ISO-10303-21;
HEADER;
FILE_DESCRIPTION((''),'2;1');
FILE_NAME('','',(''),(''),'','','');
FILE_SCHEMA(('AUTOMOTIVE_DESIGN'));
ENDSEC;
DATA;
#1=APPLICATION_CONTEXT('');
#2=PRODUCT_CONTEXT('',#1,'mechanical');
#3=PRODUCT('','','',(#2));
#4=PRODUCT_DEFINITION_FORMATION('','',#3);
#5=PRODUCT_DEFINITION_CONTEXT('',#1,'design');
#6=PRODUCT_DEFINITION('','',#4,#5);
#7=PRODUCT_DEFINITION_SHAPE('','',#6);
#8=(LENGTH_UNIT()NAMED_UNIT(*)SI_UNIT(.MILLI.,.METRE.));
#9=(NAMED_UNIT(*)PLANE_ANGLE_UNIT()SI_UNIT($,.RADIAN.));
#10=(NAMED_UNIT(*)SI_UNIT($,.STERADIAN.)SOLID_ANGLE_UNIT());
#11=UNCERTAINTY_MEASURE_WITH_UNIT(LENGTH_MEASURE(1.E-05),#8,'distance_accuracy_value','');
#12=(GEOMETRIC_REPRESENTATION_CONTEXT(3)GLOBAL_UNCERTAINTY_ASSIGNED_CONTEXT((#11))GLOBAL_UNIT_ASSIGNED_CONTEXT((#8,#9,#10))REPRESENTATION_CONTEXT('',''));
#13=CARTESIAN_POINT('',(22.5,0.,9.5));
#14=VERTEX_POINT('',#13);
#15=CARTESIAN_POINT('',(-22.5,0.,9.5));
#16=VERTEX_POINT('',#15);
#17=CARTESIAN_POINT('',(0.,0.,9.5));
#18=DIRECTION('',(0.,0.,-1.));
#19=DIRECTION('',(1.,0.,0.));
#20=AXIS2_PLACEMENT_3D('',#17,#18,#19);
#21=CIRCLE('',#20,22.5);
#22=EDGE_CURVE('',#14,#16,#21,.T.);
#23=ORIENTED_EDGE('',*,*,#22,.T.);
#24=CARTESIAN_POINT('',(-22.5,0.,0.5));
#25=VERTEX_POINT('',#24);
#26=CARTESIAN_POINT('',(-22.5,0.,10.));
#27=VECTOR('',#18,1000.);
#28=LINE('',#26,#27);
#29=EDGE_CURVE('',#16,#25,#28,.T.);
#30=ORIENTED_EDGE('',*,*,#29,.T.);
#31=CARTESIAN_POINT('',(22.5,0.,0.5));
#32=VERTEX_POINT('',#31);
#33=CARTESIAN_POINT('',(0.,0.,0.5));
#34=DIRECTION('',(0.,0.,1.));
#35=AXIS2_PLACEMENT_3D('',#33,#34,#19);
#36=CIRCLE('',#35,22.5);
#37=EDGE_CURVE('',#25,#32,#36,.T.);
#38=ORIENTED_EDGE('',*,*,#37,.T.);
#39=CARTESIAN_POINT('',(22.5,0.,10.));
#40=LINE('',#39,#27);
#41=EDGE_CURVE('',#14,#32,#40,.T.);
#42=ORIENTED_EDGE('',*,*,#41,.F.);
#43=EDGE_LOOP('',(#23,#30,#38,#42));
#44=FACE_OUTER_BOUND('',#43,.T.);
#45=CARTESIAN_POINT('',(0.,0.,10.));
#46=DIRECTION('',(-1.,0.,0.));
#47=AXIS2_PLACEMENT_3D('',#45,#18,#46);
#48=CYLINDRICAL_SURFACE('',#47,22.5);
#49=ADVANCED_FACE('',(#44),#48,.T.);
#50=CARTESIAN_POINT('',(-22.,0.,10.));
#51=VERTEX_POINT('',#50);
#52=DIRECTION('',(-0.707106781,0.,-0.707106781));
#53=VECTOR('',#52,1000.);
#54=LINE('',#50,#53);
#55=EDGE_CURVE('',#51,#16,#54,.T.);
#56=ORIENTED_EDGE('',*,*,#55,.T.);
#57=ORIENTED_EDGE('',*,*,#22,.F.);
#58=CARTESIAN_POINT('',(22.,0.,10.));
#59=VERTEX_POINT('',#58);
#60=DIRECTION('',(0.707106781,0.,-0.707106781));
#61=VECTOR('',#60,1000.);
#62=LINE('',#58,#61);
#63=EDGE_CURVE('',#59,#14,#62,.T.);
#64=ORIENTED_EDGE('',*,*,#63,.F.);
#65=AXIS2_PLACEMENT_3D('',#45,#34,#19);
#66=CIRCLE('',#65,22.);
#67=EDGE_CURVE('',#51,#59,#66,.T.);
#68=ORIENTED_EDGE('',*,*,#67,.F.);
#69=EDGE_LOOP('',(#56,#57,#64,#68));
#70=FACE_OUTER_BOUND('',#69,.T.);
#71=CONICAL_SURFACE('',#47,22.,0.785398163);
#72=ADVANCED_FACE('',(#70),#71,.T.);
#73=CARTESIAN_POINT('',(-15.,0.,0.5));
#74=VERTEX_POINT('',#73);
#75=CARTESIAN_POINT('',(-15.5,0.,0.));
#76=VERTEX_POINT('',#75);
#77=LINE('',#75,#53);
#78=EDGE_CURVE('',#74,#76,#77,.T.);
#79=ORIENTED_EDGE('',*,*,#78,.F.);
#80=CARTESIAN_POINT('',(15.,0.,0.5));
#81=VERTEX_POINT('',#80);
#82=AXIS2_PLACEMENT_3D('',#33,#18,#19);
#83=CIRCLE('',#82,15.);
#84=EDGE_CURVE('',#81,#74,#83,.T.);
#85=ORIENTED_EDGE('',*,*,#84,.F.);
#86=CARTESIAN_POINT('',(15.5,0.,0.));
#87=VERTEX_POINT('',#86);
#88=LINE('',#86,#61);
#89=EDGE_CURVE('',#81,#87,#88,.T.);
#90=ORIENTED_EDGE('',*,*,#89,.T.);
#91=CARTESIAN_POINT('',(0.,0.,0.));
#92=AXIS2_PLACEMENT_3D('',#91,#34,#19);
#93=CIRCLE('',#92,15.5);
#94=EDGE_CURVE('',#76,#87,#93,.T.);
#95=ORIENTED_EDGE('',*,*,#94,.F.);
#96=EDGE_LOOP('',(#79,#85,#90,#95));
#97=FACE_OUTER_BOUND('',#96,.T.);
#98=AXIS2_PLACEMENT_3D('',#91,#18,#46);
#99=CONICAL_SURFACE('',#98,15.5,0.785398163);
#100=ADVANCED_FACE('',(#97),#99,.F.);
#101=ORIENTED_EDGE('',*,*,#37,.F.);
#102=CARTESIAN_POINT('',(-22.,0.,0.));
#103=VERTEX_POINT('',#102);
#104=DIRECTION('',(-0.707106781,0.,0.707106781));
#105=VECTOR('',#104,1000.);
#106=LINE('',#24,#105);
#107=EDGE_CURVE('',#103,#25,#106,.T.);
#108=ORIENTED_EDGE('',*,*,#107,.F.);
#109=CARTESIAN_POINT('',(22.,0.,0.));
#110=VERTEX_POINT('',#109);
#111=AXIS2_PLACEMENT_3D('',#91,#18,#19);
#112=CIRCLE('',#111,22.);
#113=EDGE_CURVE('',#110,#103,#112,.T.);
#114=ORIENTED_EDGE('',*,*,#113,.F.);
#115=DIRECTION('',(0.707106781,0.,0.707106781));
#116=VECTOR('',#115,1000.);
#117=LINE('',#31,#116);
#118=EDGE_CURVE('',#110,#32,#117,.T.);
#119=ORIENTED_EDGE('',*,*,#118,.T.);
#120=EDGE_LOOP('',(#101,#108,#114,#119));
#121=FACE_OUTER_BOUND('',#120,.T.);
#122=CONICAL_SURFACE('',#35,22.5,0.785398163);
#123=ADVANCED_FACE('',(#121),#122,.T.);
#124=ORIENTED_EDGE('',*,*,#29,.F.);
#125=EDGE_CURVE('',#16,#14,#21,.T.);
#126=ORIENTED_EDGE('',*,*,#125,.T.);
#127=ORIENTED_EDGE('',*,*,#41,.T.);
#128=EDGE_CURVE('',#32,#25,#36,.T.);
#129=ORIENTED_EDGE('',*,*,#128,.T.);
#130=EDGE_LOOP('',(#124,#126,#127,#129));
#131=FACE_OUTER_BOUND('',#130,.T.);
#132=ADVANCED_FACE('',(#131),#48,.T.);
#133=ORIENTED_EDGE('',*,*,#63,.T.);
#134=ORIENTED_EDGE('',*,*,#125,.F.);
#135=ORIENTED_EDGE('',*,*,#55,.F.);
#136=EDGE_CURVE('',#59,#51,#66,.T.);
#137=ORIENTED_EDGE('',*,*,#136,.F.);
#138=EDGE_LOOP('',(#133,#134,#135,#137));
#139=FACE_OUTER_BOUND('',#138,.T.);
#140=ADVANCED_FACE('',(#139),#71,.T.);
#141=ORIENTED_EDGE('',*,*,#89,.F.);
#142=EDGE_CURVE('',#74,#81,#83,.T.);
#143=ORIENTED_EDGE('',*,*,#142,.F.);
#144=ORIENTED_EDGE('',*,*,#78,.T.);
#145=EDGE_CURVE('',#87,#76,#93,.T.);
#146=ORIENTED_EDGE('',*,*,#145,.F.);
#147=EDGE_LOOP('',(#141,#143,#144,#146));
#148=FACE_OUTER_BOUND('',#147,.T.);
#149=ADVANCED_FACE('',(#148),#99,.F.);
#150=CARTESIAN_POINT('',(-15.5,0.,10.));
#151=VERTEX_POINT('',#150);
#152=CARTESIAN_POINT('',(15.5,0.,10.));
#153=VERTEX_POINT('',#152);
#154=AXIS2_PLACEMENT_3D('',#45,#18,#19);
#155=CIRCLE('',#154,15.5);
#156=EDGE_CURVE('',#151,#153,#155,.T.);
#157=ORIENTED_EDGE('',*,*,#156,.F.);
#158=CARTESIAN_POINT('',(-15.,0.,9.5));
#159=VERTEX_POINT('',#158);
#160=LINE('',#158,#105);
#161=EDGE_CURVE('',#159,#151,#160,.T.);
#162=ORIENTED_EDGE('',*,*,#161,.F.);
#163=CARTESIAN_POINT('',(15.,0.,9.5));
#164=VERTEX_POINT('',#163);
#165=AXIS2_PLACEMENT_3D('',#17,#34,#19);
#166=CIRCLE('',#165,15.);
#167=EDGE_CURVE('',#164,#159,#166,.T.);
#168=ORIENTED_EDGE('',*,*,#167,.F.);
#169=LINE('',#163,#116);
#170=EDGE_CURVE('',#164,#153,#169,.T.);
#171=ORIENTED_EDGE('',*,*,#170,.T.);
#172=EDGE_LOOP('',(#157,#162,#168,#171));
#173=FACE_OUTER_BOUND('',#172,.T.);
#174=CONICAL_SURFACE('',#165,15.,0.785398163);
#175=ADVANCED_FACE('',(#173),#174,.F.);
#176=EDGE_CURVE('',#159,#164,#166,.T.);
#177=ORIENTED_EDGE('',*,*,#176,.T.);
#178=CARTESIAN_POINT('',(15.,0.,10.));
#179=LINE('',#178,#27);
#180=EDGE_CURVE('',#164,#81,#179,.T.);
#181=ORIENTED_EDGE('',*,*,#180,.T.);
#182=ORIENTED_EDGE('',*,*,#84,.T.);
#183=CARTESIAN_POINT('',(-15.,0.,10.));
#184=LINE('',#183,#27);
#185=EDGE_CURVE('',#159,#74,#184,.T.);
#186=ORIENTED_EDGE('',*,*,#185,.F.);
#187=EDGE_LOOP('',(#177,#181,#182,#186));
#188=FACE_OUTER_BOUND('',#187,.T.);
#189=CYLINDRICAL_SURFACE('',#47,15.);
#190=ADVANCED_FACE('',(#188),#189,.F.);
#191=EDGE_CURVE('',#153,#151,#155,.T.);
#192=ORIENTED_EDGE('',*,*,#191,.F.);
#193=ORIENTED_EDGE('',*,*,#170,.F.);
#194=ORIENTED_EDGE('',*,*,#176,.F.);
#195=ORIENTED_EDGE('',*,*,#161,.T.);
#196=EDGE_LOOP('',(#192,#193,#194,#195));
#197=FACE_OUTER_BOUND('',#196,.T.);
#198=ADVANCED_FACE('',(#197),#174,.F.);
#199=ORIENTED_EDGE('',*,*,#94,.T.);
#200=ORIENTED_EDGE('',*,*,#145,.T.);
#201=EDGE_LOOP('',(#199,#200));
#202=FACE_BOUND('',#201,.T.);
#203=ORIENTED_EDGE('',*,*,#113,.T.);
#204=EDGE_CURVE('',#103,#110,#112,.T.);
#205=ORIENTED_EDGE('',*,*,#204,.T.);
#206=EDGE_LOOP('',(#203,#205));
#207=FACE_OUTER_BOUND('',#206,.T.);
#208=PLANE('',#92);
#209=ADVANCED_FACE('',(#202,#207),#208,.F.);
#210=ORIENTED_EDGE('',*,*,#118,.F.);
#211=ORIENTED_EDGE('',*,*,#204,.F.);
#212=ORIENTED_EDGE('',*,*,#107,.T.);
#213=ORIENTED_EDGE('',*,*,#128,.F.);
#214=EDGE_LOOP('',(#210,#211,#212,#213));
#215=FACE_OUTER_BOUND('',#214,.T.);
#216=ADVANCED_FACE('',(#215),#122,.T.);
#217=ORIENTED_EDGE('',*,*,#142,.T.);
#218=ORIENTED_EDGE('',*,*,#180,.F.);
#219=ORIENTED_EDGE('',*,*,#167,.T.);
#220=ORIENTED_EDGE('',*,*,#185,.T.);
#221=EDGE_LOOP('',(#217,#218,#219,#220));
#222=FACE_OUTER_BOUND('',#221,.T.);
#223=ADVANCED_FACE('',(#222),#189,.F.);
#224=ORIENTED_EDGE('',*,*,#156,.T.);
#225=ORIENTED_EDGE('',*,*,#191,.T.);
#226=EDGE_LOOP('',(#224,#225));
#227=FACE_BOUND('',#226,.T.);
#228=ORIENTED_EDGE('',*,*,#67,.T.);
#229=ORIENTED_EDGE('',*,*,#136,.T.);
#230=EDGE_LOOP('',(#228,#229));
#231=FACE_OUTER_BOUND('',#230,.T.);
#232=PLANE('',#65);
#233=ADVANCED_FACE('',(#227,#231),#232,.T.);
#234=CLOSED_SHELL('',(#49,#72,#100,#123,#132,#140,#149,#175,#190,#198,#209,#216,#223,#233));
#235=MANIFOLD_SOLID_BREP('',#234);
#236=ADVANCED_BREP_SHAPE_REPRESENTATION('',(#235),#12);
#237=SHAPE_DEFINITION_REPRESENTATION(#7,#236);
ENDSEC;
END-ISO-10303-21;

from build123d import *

# Parameters (mm, degrees)
SKETCH1_R           = 22.5
SKETCH1_R_2         = 15
BOSS_EXTRUDE1_DEPTH = 10
CHAMFER1_SIZE       = 0.5


with BuildPart() as part:
    # Sketch1 → Boss-Extrude1 (new body)
    with BuildSketch(Plane.XY):
        Circle(SKETCH1_R)
        Circle(SKETCH1_R_2, mode=Mode.SUBTRACT)
    extrude(amount=BOSS_EXTRUDE1_DEPTH)

    # Chamfer1
    chamfer1_edges = [part.edges().sort_by_distance(p)[0] for p in [
        (-22.5, 0, 0),
        (-22.5, 0, 10),
        (-15, 0, 0),
        (-15, 0, 10),
    ]]
    chamfer(chamfer1_edges, length=CHAMFER1_SIZE)


solid = part.part
